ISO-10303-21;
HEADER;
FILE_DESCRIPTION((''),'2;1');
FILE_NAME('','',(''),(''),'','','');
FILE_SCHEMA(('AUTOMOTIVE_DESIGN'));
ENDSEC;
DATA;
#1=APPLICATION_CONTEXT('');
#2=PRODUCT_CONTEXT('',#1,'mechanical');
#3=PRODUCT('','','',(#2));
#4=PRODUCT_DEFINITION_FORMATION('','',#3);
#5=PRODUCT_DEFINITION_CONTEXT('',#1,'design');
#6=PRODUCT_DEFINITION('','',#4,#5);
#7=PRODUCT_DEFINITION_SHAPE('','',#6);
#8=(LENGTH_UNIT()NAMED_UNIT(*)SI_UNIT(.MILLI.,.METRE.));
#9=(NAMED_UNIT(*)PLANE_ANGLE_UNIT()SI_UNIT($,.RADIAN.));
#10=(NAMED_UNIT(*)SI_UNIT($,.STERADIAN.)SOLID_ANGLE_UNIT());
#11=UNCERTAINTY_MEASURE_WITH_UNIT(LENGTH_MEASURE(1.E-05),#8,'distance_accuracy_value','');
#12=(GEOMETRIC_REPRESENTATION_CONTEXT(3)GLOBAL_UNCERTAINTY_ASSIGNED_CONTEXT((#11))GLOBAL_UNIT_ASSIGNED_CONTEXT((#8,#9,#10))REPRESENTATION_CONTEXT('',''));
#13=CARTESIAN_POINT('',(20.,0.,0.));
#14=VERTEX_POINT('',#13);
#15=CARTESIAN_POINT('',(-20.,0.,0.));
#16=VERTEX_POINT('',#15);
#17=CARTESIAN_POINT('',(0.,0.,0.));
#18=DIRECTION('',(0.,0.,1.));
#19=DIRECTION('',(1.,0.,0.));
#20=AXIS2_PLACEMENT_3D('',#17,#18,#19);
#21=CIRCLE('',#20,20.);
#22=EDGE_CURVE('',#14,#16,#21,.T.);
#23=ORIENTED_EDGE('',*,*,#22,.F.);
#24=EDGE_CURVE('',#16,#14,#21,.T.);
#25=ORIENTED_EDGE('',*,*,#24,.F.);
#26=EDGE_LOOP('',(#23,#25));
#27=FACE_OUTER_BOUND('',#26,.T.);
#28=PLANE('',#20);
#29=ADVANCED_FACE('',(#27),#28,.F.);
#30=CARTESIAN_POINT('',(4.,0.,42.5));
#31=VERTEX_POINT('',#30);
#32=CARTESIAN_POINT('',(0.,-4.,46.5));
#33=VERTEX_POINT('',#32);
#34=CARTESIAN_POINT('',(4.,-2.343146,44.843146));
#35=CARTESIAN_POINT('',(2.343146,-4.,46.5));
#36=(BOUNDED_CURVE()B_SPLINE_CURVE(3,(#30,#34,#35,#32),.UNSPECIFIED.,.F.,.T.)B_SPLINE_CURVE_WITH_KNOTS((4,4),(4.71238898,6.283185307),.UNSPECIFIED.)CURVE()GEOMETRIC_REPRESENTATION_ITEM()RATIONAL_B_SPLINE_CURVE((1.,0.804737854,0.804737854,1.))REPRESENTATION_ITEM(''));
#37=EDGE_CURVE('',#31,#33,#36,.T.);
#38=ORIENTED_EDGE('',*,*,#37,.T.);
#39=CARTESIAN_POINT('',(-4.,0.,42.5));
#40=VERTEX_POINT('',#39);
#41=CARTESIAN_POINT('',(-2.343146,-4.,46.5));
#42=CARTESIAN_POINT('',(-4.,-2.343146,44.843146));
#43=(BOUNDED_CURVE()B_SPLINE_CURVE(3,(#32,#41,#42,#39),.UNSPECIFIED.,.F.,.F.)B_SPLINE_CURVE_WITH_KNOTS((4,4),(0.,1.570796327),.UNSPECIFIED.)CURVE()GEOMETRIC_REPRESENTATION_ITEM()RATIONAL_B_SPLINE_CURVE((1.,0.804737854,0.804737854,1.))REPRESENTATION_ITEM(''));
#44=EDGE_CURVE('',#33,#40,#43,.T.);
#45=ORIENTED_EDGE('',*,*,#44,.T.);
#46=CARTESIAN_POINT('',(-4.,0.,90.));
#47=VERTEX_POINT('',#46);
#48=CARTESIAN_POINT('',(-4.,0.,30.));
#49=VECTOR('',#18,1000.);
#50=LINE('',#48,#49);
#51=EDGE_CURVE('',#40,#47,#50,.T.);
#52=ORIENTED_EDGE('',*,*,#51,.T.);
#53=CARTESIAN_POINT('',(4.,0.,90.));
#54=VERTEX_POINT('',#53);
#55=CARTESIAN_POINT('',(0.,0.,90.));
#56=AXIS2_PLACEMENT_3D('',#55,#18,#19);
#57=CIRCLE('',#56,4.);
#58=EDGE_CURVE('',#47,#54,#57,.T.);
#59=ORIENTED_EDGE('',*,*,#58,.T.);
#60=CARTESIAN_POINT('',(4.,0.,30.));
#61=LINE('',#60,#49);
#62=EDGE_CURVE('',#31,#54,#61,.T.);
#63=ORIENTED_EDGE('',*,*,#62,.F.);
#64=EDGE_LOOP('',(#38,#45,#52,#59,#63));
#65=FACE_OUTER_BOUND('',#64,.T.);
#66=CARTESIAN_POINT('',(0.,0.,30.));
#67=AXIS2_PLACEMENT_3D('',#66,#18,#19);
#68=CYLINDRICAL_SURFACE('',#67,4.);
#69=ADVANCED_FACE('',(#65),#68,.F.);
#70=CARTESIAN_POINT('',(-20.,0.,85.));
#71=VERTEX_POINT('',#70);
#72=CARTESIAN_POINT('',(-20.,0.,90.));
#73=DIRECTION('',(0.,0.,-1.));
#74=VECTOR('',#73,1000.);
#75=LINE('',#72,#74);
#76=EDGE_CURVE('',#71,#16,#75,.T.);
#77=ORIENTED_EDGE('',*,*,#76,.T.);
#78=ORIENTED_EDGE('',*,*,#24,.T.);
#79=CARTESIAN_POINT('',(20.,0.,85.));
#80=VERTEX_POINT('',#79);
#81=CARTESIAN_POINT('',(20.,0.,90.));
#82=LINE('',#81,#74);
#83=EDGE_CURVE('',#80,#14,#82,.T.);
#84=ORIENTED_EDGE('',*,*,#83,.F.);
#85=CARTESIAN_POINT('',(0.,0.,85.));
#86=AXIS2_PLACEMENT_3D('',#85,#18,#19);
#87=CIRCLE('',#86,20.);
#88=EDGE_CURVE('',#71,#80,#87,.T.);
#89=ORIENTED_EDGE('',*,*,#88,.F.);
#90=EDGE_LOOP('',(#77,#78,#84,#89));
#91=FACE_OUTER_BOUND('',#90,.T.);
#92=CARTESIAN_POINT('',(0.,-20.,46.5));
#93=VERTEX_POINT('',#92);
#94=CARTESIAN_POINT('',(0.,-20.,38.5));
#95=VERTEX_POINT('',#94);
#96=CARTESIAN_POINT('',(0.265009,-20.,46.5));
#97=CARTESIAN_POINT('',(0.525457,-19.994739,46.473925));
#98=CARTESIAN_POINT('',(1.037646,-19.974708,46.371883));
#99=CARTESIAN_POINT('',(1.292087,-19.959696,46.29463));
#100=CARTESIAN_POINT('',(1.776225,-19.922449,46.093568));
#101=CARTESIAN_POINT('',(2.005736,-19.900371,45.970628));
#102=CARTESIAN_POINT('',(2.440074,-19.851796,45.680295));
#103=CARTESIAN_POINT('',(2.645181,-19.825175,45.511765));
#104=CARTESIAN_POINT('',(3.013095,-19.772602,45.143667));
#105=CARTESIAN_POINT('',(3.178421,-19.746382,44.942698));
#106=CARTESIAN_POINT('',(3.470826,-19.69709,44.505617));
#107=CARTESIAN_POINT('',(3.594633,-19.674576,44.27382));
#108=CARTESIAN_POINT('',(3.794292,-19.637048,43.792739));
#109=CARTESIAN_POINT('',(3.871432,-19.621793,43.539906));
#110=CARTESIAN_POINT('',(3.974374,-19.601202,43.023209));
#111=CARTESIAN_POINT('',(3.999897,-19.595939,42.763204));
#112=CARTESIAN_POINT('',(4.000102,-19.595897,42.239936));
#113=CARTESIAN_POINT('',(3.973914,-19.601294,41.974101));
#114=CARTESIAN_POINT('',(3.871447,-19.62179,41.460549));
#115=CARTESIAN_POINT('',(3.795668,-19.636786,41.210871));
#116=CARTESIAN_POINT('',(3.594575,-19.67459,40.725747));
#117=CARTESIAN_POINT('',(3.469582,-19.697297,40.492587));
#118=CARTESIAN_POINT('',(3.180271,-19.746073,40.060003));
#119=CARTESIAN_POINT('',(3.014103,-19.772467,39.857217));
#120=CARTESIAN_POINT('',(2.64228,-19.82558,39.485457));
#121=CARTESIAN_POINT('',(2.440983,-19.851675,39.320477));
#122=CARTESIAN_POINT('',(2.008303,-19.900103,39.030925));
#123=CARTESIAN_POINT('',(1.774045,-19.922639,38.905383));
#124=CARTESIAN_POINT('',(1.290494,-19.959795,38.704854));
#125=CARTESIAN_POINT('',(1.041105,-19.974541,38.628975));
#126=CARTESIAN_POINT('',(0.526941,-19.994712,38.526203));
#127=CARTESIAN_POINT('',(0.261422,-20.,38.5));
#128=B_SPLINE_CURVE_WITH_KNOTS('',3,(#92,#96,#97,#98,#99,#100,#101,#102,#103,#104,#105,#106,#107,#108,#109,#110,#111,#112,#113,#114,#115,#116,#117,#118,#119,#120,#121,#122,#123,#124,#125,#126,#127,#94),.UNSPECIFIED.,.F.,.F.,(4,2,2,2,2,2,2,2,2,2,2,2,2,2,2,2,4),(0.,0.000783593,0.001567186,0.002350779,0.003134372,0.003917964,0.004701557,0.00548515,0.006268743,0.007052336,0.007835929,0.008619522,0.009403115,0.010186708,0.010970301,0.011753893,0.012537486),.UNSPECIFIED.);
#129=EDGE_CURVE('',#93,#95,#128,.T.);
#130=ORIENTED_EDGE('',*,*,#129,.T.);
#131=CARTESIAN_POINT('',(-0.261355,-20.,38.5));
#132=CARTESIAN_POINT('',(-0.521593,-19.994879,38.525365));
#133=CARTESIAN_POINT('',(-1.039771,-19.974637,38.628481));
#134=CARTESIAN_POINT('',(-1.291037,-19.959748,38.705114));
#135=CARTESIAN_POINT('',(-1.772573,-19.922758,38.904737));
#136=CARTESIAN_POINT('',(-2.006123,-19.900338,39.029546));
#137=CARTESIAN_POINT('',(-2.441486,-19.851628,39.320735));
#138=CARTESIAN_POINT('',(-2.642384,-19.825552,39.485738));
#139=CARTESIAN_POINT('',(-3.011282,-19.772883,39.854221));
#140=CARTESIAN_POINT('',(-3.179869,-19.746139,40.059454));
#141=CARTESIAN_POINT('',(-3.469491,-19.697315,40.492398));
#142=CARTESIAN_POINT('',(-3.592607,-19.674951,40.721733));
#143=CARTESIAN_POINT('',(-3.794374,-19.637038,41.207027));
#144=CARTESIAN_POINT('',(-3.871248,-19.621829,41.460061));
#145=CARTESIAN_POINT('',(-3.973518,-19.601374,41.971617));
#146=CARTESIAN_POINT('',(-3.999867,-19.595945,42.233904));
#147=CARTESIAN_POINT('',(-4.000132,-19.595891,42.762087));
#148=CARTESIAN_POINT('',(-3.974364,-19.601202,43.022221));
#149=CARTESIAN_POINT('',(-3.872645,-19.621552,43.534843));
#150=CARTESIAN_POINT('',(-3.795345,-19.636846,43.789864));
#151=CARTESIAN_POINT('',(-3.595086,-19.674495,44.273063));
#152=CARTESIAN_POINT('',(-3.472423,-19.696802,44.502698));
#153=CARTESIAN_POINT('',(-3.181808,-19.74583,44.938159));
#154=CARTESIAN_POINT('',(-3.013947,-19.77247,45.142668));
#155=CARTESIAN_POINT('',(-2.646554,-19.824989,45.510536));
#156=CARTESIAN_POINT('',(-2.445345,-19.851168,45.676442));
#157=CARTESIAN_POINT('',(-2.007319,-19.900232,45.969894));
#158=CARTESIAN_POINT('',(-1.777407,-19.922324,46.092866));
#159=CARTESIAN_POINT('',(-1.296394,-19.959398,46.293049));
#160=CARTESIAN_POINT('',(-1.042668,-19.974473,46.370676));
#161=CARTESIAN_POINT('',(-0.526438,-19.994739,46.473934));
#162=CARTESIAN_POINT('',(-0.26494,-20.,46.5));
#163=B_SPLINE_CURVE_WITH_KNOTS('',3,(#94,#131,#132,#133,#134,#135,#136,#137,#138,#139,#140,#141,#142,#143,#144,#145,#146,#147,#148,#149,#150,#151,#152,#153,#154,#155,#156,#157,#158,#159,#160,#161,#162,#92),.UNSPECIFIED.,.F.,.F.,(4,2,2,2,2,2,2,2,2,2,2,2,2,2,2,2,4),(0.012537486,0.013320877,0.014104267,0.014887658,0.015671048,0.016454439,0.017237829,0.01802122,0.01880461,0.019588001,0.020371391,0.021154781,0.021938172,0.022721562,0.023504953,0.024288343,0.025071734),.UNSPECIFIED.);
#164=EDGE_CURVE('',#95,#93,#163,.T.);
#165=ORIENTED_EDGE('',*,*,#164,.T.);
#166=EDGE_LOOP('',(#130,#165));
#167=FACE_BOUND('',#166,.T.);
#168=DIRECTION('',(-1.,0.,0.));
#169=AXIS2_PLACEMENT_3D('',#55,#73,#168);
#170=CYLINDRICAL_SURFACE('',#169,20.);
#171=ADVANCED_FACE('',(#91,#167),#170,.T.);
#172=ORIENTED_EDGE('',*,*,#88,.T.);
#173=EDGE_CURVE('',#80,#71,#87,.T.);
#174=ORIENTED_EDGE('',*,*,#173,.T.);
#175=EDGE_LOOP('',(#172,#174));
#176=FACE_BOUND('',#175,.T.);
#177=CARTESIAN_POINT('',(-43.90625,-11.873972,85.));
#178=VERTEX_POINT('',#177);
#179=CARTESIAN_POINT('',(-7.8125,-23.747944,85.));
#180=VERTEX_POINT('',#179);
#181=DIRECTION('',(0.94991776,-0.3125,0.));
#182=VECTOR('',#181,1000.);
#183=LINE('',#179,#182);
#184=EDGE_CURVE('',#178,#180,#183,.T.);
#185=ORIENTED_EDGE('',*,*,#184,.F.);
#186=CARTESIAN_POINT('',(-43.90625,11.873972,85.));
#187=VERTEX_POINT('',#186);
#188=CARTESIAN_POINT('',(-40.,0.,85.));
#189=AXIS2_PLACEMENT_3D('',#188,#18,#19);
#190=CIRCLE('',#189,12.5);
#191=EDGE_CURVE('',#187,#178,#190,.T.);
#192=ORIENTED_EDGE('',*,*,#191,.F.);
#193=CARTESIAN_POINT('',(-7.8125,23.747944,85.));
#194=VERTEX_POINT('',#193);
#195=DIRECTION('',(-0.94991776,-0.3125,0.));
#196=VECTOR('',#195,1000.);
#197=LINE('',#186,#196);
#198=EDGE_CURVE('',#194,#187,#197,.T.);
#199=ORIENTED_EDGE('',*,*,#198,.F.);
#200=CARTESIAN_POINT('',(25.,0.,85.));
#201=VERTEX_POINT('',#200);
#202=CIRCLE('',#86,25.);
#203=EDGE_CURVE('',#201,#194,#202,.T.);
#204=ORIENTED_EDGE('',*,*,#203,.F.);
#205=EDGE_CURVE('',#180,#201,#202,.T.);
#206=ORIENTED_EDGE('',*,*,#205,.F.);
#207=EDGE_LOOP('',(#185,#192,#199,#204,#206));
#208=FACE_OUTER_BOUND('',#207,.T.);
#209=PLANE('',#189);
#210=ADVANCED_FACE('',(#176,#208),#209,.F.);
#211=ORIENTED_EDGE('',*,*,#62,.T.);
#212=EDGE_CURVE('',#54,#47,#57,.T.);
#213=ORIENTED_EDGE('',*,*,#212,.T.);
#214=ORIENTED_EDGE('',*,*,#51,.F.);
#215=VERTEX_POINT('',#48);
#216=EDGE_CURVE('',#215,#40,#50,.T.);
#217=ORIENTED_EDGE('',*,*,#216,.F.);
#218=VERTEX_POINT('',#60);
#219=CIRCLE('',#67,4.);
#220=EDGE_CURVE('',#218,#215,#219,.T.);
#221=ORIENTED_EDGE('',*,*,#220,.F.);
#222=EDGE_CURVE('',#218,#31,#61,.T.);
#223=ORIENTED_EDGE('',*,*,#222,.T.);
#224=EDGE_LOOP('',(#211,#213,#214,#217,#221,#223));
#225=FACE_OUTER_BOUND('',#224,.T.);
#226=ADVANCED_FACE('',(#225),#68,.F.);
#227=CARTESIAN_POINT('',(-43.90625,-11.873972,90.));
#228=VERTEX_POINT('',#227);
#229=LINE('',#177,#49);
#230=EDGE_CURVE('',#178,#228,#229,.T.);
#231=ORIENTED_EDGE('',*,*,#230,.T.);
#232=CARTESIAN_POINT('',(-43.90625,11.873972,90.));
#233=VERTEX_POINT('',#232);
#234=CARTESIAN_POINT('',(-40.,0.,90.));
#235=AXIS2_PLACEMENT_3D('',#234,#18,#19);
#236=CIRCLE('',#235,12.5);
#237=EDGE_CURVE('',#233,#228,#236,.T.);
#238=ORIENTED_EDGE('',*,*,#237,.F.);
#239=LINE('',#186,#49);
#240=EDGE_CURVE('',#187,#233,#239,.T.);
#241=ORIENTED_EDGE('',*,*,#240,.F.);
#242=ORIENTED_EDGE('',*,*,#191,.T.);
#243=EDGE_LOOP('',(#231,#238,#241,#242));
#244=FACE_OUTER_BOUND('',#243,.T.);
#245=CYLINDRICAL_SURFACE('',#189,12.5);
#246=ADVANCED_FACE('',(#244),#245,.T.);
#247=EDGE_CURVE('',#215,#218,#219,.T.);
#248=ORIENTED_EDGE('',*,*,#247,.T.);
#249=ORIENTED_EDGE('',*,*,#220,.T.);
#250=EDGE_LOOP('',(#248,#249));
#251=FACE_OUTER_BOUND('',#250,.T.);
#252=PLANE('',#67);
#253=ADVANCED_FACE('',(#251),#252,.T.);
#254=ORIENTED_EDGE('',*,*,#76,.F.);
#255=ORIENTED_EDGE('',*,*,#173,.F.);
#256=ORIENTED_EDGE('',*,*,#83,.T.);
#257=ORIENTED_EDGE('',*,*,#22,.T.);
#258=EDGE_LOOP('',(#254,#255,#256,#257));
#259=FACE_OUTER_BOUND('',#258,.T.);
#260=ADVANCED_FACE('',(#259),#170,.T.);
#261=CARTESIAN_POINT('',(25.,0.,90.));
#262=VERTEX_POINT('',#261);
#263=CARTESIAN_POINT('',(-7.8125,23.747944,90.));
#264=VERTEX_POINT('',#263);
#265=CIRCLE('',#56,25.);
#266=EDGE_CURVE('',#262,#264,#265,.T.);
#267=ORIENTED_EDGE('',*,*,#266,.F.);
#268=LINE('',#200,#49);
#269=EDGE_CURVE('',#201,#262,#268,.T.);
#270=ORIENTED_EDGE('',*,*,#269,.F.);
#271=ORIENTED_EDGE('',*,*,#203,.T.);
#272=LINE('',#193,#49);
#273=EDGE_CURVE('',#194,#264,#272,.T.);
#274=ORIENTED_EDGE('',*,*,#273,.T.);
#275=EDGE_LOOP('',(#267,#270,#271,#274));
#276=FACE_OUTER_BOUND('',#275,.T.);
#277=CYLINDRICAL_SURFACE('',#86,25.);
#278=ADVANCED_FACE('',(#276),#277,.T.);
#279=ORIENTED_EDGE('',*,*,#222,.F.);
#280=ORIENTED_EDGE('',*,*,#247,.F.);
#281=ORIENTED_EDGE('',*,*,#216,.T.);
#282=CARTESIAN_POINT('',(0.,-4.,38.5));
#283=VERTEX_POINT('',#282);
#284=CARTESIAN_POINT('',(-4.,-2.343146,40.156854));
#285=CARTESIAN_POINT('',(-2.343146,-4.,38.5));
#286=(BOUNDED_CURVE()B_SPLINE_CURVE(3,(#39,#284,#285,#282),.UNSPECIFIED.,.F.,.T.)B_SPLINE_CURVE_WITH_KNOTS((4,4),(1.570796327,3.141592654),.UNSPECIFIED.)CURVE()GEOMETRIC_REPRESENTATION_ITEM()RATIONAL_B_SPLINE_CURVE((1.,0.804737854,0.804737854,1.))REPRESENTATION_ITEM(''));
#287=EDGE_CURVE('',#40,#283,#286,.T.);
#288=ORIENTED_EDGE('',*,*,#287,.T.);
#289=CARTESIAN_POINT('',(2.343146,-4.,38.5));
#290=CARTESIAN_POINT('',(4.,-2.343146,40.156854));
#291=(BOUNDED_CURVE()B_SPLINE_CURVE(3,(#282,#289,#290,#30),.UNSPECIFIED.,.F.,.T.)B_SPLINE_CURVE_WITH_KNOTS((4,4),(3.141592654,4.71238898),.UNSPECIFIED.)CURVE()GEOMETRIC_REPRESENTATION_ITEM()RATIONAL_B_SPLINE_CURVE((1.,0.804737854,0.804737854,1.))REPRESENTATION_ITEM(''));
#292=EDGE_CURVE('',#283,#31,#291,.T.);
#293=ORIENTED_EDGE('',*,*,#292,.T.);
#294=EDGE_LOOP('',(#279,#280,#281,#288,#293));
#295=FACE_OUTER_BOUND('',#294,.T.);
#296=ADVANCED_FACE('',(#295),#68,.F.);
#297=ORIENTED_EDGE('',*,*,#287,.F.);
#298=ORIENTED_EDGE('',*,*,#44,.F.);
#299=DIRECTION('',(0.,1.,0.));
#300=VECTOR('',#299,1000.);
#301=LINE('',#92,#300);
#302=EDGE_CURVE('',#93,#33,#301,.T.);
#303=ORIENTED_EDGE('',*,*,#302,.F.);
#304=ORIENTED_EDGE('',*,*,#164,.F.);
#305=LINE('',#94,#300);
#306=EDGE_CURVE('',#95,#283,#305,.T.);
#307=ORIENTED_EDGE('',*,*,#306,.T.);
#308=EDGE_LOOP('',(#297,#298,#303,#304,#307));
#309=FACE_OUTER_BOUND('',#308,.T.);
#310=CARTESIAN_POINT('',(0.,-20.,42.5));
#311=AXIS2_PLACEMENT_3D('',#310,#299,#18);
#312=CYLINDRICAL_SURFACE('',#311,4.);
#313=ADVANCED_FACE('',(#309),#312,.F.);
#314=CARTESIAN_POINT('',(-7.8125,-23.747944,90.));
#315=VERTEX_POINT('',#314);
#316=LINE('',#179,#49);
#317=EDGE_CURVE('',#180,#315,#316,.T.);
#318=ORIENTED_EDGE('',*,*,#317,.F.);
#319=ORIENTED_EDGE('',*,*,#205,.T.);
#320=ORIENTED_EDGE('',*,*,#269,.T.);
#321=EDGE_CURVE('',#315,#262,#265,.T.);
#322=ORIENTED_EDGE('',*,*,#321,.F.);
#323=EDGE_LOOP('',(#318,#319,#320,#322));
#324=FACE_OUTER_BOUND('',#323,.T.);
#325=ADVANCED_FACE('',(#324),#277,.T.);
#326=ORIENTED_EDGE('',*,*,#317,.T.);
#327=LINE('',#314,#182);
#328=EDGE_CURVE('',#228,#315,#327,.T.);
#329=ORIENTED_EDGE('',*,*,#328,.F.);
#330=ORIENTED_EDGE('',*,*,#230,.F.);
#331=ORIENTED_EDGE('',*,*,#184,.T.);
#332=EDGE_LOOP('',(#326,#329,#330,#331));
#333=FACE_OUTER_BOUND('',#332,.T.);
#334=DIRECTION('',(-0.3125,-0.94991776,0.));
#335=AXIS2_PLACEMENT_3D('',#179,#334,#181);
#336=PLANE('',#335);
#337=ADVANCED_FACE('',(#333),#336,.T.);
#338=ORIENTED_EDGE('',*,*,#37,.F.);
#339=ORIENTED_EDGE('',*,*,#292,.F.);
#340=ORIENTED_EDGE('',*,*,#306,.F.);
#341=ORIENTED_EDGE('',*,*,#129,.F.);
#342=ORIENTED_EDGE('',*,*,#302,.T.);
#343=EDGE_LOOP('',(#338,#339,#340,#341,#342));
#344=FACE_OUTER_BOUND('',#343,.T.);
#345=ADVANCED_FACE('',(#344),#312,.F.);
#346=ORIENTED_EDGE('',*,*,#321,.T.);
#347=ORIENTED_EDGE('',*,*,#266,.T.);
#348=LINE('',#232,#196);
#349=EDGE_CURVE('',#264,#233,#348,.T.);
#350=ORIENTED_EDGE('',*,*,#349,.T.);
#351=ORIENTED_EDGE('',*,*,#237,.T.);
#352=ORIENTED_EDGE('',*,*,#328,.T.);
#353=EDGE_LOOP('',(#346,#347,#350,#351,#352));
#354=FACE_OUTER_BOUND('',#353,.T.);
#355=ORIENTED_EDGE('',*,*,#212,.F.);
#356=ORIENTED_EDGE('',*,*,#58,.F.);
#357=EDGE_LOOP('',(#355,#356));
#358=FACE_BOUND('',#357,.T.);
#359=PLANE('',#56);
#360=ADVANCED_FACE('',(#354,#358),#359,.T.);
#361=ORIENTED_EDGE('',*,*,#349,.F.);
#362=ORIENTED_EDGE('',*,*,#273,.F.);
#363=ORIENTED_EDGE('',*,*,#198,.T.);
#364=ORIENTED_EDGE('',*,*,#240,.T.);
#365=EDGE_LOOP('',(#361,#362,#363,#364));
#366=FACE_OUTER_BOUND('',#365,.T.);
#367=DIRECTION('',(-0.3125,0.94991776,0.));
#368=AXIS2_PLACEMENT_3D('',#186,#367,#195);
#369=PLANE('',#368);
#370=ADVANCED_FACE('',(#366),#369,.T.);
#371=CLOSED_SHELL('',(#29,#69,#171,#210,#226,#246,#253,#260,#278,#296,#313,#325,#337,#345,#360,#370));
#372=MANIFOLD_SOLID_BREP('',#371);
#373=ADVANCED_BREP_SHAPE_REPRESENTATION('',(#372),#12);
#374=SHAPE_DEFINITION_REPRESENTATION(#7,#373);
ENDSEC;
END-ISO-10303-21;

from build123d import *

# Parameters (mm, degrees)
SKETCH_1_R          = 20
EXTRUDE_1_DEPTH     = 90
EXTRUDE_2_DEPTH     = 5
SKETCH_3_R          = 4
CUT_EXTRUDE_1_DEPTH = 60
CUT_EXTRUDE_2_DEPTH = 20


with BuildPart() as part:
    # 草图1 → 凸台-拉伸1 (new body)
    with BuildSketch(Plane.XY):
        with Locations(Location((0, 0, 0), (0, 0, 180))):
            Circle(SKETCH_1_R)
    extrude(amount=EXTRUDE_1_DEPTH)

    # 草图2 → 凸台-拉伸2 (add)
    with BuildSketch(Plane.XY.offset(90)):
        with BuildLine():
            Line((-43.90625, 11.873971995), (-7.8125, 23.74794399))
            ThreePointArc((-7.8125, 23.74794399), (25, 0), (-7.8125, -23.74794399))
            Line((-7.8125, -23.74794399), (-43.90625, -11.873971995))
            ThreePointArc((-43.90625, -11.873971995), (-52.5, 0), (-43.90625, 11.873971995))
        make_face()
    extrude(amount=-EXTRUDE_2_DEPTH)

    # 草图3 → 切除-拉伸1 (cut)
    with BuildSketch(Plane.XY.offset(90)):
        Circle(SKETCH_3_R)
    extrude(amount=-CUT_EXTRUDE_1_DEPTH, mode=Mode.SUBTRACT)

    # 草图4 → 切除-拉伸2 (cut)
    with BuildSketch(Plane(origin=(0, 0, 0), x_dir=(1, 0, 0), z_dir=(0, 1, 0))):
        with BuildLine():
            ThreePointArc((4, -42.5), (2.828427125, -39.671572875), (0, -38.5))
            Line((0, -38.5), (0, -46.5))
            ThreePointArc((0, -46.5), (2.828427125, -45.328427125), (4, -42.5))
        make_face()
        with BuildLine():
            Line((0, -46.5), (0, -38.5))
            ThreePointArc((0, -38.5), (-4, -42.5), (0, -46.5))
        make_face()
    extrude(amount=-CUT_EXTRUDE_2_DEPTH, mode=Mode.SUBTRACT)


solid = part.part
